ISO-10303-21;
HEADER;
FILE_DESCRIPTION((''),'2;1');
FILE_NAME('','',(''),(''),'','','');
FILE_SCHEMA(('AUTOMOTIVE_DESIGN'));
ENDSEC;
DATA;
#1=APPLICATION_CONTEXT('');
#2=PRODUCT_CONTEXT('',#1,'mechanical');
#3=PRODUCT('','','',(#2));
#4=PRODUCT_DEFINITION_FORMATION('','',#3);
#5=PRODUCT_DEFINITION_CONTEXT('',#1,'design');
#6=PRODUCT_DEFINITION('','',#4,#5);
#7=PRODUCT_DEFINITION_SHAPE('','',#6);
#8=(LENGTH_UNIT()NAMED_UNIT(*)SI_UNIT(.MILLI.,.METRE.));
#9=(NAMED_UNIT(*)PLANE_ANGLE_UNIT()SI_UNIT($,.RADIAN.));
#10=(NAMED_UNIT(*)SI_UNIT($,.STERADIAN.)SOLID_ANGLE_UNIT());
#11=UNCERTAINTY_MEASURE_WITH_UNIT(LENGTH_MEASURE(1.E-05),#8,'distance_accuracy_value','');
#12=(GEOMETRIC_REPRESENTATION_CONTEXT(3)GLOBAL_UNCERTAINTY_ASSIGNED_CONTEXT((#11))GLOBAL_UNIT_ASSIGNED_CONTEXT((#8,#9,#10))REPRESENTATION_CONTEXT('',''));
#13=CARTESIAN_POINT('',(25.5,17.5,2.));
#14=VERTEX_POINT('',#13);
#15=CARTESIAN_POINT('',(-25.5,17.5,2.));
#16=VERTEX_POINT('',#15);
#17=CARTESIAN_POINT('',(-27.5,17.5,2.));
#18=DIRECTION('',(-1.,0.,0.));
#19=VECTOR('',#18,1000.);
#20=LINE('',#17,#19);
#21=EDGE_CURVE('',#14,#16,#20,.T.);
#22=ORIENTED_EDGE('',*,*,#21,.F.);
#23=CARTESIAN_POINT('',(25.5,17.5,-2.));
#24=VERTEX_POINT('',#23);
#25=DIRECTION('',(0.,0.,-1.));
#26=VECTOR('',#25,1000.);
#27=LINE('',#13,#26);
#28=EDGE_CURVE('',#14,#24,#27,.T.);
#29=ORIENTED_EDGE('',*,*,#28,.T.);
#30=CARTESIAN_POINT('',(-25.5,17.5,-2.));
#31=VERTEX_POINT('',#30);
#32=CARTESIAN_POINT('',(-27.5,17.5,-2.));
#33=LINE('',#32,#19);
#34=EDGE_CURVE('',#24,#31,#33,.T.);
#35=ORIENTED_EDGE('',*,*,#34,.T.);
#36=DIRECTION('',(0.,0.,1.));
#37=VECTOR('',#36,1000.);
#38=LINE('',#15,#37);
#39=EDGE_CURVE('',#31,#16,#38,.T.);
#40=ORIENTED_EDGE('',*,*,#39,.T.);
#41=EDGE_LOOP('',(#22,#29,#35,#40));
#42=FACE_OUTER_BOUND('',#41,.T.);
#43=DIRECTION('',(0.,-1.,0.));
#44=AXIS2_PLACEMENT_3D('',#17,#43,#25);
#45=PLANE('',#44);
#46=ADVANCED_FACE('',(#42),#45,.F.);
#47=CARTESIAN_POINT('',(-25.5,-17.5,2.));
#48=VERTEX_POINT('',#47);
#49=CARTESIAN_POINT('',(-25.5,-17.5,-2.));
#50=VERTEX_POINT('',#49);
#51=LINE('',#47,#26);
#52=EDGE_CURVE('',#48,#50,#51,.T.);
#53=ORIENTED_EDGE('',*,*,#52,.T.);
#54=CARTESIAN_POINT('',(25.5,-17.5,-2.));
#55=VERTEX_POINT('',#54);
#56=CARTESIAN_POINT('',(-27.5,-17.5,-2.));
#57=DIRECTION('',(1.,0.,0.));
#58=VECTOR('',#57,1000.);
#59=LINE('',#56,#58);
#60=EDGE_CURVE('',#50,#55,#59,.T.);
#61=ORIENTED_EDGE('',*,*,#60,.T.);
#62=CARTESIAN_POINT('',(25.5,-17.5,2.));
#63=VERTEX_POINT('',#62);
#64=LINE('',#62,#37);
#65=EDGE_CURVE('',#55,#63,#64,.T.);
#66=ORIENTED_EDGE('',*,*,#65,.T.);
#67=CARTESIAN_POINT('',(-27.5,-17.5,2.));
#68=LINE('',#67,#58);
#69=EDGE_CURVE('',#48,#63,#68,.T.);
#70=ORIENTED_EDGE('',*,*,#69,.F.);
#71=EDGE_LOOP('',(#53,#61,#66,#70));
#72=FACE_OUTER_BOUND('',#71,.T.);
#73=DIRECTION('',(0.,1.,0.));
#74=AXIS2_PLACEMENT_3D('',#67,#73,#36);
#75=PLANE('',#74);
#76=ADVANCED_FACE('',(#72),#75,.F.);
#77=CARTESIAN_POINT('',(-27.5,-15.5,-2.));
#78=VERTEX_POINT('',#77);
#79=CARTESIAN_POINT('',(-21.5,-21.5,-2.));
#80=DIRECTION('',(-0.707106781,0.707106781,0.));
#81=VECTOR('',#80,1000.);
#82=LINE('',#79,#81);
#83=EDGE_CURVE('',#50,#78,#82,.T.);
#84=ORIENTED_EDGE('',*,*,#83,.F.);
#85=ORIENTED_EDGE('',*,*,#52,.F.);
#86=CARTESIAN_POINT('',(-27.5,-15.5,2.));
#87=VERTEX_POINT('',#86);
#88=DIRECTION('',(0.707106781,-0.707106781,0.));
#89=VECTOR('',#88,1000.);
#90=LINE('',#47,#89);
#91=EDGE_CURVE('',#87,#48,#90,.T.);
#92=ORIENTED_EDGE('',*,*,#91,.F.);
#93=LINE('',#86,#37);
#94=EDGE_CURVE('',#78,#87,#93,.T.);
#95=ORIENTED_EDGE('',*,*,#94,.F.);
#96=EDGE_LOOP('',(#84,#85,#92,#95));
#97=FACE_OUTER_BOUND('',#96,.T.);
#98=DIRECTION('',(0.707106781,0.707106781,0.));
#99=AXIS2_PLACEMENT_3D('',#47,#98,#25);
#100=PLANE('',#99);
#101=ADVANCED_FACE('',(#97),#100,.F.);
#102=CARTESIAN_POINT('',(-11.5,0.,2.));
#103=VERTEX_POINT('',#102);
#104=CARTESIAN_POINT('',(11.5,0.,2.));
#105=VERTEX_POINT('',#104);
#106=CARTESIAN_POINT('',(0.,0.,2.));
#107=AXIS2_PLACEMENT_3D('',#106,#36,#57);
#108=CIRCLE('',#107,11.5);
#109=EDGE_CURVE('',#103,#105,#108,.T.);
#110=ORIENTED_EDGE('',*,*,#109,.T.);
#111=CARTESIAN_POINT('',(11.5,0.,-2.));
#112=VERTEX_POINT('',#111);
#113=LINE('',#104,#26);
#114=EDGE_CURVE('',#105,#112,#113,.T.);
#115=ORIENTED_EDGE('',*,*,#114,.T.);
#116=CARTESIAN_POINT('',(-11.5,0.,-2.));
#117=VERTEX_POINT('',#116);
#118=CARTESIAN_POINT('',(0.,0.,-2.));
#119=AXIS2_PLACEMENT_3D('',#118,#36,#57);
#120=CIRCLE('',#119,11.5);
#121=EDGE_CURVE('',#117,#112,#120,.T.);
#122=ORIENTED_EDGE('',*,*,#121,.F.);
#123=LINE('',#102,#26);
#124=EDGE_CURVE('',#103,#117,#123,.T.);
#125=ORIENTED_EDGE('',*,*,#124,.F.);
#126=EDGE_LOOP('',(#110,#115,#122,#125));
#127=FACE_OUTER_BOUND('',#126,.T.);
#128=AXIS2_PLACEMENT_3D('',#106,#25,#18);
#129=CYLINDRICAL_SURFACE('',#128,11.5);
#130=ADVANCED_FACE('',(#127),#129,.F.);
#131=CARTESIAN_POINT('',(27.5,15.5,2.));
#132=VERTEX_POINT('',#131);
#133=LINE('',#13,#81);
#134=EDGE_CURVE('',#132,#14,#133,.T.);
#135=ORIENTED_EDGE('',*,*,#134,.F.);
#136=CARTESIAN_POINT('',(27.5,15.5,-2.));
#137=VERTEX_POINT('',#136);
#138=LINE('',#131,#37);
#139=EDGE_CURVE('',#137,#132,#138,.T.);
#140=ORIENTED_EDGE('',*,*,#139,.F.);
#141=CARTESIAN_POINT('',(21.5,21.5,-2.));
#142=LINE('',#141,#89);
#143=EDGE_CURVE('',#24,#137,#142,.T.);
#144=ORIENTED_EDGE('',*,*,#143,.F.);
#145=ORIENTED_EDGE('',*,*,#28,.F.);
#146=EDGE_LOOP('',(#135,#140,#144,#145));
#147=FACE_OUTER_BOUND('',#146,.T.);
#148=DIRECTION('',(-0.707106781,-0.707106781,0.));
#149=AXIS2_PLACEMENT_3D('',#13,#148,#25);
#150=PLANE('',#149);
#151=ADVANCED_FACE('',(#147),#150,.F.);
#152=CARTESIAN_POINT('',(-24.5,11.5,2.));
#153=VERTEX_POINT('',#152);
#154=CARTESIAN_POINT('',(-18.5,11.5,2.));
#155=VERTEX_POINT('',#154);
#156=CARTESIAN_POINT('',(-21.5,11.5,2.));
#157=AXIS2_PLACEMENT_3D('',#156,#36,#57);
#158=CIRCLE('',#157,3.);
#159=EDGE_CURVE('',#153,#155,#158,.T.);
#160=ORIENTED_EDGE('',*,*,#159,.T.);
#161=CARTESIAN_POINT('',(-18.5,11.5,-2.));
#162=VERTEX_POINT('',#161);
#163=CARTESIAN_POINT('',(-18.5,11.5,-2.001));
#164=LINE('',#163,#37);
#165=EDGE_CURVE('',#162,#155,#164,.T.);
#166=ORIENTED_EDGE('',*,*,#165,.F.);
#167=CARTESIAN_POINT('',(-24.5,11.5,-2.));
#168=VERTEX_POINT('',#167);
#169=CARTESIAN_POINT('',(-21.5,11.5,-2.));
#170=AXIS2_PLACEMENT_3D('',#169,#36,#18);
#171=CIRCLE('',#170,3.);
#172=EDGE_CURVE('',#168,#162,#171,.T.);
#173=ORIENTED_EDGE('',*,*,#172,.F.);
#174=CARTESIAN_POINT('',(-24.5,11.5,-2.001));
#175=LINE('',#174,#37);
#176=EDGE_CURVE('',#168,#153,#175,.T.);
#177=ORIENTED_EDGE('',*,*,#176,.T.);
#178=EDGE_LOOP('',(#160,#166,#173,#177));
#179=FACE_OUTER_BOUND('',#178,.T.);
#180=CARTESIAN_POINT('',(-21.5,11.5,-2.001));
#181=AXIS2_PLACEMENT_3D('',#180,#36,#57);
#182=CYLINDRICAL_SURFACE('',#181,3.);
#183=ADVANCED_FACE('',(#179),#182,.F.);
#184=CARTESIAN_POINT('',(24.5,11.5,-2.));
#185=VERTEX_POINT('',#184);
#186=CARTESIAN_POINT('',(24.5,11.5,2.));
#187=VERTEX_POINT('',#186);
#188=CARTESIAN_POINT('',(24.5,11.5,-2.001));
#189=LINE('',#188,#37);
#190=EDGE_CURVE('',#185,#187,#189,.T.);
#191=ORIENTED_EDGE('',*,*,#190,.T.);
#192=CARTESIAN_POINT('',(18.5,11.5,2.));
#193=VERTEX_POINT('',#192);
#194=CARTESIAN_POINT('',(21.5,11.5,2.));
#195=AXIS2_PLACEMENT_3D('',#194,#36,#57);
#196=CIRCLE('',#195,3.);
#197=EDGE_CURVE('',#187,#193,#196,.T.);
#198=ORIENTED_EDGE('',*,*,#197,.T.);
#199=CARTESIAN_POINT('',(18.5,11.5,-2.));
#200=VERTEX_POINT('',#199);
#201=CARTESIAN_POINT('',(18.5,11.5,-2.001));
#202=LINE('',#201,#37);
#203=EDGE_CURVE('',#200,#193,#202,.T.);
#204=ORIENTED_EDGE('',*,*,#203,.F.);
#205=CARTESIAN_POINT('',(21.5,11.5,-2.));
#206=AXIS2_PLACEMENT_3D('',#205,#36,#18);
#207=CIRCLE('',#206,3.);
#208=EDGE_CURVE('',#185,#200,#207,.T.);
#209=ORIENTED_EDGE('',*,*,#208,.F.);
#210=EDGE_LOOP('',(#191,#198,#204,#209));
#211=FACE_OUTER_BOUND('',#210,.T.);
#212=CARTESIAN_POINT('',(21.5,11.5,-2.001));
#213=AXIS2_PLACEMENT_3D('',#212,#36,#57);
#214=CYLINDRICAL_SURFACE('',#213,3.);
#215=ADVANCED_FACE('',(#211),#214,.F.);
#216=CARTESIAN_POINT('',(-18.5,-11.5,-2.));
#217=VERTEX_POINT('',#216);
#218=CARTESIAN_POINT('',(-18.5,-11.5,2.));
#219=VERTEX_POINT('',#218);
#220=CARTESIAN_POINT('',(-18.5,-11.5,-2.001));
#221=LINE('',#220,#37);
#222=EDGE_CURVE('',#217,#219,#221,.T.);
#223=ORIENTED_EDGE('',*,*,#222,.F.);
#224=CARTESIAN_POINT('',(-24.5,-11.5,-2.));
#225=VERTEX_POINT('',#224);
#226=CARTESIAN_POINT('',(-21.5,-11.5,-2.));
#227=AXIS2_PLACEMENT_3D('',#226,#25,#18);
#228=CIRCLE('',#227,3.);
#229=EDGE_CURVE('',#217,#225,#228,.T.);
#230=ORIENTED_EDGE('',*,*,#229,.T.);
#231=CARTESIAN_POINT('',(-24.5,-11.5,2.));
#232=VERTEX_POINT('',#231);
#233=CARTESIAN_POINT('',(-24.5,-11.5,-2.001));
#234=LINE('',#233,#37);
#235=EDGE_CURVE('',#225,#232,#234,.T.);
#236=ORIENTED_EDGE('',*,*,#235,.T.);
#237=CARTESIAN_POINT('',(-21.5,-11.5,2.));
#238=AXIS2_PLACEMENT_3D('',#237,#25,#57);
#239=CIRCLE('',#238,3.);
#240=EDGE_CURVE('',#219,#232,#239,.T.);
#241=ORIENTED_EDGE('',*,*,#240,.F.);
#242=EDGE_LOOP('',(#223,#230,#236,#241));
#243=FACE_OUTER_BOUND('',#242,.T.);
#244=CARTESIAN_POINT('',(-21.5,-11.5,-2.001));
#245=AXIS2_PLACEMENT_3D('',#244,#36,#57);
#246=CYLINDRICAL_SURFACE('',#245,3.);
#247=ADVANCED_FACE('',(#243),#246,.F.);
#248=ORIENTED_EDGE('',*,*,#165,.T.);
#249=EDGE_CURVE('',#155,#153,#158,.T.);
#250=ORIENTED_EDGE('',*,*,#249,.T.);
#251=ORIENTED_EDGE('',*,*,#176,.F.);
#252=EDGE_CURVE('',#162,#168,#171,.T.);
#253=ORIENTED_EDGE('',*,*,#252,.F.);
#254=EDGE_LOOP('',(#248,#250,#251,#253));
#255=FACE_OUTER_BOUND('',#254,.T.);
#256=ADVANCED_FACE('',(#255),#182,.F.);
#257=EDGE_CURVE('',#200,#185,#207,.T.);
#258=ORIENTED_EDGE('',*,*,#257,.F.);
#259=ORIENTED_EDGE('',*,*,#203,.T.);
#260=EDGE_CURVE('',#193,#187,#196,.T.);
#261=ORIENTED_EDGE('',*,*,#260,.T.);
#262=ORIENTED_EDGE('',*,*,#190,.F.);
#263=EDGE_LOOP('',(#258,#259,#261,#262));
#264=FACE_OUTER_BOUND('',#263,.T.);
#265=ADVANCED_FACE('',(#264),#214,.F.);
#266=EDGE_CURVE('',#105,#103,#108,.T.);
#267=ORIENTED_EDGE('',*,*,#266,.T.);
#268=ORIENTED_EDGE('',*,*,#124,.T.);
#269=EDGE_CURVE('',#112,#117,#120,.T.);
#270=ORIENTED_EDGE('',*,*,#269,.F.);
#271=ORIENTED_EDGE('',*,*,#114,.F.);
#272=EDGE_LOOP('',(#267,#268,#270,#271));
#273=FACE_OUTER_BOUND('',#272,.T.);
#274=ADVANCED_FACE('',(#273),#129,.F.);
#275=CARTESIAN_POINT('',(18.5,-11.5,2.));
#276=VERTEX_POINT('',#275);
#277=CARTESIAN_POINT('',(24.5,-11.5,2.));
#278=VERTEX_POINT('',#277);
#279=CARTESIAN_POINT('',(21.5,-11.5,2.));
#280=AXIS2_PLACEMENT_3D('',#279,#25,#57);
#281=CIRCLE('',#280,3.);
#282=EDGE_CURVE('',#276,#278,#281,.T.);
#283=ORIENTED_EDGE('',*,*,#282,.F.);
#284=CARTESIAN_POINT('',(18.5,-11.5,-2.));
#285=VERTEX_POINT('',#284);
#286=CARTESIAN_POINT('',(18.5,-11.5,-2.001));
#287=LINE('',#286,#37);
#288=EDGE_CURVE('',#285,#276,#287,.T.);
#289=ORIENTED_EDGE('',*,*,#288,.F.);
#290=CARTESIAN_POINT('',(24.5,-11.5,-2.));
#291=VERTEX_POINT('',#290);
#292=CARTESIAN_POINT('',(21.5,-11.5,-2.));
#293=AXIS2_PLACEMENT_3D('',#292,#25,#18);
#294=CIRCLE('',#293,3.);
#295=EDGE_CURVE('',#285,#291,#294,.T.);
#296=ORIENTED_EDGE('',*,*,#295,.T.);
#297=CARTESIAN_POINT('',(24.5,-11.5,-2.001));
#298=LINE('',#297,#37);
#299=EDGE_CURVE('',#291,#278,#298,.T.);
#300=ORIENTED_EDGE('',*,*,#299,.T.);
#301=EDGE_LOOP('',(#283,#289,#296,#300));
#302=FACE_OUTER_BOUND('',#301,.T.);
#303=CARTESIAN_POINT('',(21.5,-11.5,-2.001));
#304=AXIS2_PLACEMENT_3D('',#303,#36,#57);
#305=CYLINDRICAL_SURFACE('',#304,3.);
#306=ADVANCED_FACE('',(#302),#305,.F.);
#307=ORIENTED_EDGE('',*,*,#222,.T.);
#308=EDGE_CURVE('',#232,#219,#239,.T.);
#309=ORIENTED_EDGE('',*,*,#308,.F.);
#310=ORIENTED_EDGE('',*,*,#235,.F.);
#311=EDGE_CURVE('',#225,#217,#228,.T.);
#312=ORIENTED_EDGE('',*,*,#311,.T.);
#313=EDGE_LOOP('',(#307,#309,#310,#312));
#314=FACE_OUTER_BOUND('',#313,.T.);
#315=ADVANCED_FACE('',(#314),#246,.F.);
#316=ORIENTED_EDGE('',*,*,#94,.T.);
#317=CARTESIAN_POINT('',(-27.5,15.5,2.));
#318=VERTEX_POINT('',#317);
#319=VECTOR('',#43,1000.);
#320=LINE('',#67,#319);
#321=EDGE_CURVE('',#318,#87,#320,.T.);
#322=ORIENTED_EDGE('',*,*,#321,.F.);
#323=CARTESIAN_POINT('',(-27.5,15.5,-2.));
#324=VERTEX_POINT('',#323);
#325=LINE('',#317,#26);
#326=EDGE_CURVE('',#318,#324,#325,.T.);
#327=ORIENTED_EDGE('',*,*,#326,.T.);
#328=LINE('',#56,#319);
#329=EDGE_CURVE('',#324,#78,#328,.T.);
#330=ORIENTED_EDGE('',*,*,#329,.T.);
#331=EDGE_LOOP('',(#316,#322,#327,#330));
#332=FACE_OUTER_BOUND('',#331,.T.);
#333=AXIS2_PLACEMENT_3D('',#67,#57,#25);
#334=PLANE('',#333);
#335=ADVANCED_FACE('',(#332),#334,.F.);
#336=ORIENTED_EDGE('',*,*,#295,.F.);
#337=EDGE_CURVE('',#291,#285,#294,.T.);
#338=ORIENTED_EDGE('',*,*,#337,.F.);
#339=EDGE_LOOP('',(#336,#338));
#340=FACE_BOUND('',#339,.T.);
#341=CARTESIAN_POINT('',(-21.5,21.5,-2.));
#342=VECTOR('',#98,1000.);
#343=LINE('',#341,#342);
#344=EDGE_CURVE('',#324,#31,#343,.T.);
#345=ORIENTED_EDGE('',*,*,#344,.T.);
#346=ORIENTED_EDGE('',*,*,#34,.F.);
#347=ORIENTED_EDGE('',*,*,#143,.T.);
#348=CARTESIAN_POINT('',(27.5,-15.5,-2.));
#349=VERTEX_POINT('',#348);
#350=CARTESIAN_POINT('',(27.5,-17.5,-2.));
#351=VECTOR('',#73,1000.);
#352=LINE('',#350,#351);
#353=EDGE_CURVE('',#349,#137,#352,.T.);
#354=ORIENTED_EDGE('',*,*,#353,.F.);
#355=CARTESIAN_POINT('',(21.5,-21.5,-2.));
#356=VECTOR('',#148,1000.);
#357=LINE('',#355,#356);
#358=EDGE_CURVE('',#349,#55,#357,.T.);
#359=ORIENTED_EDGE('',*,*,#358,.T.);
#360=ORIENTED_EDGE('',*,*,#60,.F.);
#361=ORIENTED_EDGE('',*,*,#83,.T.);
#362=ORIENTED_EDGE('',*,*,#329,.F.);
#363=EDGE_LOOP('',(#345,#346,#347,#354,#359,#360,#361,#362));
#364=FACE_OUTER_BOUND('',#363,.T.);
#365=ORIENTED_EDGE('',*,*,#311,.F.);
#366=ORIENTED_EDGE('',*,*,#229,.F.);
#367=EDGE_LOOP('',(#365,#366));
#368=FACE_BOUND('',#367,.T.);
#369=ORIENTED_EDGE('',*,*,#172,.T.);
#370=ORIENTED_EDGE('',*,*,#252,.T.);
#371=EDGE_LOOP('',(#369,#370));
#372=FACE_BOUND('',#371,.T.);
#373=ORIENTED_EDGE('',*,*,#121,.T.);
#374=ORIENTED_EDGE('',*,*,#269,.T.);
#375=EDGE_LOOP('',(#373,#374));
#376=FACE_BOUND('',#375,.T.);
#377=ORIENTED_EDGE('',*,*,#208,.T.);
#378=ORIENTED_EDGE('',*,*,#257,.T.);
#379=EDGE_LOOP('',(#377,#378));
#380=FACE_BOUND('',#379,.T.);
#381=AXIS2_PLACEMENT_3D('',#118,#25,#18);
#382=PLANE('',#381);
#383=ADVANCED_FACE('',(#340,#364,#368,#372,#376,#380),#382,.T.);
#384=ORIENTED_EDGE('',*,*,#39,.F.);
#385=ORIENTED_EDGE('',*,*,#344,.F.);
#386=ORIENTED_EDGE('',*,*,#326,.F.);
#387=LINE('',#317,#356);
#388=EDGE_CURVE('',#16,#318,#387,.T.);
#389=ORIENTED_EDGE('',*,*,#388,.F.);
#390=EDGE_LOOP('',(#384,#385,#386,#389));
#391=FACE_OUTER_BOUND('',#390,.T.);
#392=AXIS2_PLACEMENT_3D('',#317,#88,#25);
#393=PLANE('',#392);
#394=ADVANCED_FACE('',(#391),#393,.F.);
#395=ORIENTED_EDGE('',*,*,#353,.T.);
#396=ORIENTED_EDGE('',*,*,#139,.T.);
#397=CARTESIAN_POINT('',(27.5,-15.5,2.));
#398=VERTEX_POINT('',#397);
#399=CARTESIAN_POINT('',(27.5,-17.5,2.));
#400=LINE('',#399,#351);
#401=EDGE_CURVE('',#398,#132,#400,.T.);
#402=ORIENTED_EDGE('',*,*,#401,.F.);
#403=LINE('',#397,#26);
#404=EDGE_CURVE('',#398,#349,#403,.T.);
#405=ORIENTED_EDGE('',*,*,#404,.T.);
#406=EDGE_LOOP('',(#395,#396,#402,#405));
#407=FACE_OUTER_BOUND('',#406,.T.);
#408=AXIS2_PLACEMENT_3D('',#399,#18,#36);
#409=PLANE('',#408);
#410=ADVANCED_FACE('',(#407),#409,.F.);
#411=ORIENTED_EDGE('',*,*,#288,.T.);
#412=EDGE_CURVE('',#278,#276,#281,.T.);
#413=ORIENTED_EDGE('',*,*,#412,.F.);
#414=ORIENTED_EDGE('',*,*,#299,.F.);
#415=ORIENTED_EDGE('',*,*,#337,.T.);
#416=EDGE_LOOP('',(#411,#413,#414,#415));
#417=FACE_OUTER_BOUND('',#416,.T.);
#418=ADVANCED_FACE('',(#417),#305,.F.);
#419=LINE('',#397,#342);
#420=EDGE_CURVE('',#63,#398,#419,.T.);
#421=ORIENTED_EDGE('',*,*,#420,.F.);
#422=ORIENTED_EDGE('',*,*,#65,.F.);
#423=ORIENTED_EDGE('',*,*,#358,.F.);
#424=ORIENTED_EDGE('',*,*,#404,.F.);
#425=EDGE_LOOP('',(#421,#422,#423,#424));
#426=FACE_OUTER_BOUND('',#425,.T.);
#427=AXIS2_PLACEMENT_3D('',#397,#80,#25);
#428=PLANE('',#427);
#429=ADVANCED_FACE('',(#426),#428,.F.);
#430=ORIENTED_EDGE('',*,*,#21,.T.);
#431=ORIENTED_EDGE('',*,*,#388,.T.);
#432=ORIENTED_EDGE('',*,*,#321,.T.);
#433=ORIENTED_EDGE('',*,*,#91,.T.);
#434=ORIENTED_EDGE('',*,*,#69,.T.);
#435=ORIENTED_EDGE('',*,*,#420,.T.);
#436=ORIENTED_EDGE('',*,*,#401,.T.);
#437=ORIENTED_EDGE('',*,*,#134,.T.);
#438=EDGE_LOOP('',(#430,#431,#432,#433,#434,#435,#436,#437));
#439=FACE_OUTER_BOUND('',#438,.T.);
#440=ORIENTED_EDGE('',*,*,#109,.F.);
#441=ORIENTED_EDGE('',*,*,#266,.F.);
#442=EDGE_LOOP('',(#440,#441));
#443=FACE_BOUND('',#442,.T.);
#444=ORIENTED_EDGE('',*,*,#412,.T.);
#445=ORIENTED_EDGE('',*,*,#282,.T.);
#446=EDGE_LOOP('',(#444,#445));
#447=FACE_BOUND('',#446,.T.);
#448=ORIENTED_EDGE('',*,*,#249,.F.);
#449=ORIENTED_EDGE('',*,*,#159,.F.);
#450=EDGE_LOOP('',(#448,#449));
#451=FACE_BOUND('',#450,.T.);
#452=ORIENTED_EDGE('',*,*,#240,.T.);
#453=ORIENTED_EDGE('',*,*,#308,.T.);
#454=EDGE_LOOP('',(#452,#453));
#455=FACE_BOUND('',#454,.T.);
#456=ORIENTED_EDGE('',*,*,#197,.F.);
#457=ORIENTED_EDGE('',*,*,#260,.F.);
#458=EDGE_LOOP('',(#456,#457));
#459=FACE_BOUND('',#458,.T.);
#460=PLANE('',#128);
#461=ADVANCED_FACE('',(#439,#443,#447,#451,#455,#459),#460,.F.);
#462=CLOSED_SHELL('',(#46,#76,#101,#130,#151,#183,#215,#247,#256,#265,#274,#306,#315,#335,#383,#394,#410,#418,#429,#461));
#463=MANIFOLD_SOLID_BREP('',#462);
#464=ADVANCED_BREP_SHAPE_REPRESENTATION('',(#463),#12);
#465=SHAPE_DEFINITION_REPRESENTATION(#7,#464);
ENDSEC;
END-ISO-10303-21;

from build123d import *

# Parameters (mm, degrees)
SKETCH_1_W          = 55
SKETCH_1_H          = 35
SKETCH_1_R          = 11.5
EXTRUDE_1_DEPTH     = 2
CUT_EXTRUDE_1_REACH = 34.841
SKETCH_2_R          = 3
CHAMFER_1_SIZE      = 2


with BuildPart() as part:
    # 草图1 → 凸台-拉伸1 (new, symmetric)
    with BuildSketch(Plane.XY):
        Rectangle(SKETCH_1_W, SKETCH_1_H)
        Circle(SKETCH_1_R, mode=Mode.SUBTRACT)
    extrude(amount=EXTRUDE_1_DEPTH, both=True)

    # 草图2 → 切除-拉伸1 (cut, up to next)
    with BuildSketch(Plane.XY.offset(2), mode=Mode.PRIVATE) as cut_extrude_1_sk1:
        with Locations((-21.5, 11.5)):
            Circle(SKETCH_2_R)
    cut_extrude_1_tool1 = extrude(cut_extrude_1_sk1.sketch, amount=-CUT_EXTRUDE_1_REACH, mode=Mode.PRIVATE) & part.part
    # 草图2 → 切除-拉伸1 (cut, up to next)
    with BuildSketch(Plane.XY.offset(2), mode=Mode.PRIVATE) as cut_extrude_1_sk2:
        with Locations((21.5, 11.5)):
            Circle(SKETCH_2_R)
    cut_extrude_1_tool2 = extrude(cut_extrude_1_sk2.sketch, amount=-CUT_EXTRUDE_1_REACH, mode=Mode.PRIVATE) & part.part
    cut_extrude_1_1 = cut_extrude_1_tool1.solids().sort_by_distance((-21.5, 11.5, 2))[0]
    add(cut_extrude_1_1, mode=Mode.SUBTRACT)
    cut_extrude_1_2 = cut_extrude_1_tool2.solids().sort_by_distance((21.5, 11.5, 2))[0]
    add(cut_extrude_1_2, mode=Mode.SUBTRACT)
    cut_extrude_1 = cut_extrude_1_1 + cut_extrude_1_2  # 切除-拉伸1 as one shape, for the pattern or mirror that repeats it

    # 倒角1
    chamfer_1_edges = [part.edges().sort_by_distance(p)[0] for p in [
        (27.5, -17.5, 0),
        (-27.5, -17.5, 0),
        (-27.5, 17.5, 0),
        (27.5, 17.5, 0),
    ]]
    chamfer(chamfer_1_edges, length=CHAMFER_1_SIZE)

    # 镜向1: 切除-拉伸1 across plane
    add(cut_extrude_1.mirror(Plane.ZX), mode=Mode.SUBTRACT)


solid = part.part
